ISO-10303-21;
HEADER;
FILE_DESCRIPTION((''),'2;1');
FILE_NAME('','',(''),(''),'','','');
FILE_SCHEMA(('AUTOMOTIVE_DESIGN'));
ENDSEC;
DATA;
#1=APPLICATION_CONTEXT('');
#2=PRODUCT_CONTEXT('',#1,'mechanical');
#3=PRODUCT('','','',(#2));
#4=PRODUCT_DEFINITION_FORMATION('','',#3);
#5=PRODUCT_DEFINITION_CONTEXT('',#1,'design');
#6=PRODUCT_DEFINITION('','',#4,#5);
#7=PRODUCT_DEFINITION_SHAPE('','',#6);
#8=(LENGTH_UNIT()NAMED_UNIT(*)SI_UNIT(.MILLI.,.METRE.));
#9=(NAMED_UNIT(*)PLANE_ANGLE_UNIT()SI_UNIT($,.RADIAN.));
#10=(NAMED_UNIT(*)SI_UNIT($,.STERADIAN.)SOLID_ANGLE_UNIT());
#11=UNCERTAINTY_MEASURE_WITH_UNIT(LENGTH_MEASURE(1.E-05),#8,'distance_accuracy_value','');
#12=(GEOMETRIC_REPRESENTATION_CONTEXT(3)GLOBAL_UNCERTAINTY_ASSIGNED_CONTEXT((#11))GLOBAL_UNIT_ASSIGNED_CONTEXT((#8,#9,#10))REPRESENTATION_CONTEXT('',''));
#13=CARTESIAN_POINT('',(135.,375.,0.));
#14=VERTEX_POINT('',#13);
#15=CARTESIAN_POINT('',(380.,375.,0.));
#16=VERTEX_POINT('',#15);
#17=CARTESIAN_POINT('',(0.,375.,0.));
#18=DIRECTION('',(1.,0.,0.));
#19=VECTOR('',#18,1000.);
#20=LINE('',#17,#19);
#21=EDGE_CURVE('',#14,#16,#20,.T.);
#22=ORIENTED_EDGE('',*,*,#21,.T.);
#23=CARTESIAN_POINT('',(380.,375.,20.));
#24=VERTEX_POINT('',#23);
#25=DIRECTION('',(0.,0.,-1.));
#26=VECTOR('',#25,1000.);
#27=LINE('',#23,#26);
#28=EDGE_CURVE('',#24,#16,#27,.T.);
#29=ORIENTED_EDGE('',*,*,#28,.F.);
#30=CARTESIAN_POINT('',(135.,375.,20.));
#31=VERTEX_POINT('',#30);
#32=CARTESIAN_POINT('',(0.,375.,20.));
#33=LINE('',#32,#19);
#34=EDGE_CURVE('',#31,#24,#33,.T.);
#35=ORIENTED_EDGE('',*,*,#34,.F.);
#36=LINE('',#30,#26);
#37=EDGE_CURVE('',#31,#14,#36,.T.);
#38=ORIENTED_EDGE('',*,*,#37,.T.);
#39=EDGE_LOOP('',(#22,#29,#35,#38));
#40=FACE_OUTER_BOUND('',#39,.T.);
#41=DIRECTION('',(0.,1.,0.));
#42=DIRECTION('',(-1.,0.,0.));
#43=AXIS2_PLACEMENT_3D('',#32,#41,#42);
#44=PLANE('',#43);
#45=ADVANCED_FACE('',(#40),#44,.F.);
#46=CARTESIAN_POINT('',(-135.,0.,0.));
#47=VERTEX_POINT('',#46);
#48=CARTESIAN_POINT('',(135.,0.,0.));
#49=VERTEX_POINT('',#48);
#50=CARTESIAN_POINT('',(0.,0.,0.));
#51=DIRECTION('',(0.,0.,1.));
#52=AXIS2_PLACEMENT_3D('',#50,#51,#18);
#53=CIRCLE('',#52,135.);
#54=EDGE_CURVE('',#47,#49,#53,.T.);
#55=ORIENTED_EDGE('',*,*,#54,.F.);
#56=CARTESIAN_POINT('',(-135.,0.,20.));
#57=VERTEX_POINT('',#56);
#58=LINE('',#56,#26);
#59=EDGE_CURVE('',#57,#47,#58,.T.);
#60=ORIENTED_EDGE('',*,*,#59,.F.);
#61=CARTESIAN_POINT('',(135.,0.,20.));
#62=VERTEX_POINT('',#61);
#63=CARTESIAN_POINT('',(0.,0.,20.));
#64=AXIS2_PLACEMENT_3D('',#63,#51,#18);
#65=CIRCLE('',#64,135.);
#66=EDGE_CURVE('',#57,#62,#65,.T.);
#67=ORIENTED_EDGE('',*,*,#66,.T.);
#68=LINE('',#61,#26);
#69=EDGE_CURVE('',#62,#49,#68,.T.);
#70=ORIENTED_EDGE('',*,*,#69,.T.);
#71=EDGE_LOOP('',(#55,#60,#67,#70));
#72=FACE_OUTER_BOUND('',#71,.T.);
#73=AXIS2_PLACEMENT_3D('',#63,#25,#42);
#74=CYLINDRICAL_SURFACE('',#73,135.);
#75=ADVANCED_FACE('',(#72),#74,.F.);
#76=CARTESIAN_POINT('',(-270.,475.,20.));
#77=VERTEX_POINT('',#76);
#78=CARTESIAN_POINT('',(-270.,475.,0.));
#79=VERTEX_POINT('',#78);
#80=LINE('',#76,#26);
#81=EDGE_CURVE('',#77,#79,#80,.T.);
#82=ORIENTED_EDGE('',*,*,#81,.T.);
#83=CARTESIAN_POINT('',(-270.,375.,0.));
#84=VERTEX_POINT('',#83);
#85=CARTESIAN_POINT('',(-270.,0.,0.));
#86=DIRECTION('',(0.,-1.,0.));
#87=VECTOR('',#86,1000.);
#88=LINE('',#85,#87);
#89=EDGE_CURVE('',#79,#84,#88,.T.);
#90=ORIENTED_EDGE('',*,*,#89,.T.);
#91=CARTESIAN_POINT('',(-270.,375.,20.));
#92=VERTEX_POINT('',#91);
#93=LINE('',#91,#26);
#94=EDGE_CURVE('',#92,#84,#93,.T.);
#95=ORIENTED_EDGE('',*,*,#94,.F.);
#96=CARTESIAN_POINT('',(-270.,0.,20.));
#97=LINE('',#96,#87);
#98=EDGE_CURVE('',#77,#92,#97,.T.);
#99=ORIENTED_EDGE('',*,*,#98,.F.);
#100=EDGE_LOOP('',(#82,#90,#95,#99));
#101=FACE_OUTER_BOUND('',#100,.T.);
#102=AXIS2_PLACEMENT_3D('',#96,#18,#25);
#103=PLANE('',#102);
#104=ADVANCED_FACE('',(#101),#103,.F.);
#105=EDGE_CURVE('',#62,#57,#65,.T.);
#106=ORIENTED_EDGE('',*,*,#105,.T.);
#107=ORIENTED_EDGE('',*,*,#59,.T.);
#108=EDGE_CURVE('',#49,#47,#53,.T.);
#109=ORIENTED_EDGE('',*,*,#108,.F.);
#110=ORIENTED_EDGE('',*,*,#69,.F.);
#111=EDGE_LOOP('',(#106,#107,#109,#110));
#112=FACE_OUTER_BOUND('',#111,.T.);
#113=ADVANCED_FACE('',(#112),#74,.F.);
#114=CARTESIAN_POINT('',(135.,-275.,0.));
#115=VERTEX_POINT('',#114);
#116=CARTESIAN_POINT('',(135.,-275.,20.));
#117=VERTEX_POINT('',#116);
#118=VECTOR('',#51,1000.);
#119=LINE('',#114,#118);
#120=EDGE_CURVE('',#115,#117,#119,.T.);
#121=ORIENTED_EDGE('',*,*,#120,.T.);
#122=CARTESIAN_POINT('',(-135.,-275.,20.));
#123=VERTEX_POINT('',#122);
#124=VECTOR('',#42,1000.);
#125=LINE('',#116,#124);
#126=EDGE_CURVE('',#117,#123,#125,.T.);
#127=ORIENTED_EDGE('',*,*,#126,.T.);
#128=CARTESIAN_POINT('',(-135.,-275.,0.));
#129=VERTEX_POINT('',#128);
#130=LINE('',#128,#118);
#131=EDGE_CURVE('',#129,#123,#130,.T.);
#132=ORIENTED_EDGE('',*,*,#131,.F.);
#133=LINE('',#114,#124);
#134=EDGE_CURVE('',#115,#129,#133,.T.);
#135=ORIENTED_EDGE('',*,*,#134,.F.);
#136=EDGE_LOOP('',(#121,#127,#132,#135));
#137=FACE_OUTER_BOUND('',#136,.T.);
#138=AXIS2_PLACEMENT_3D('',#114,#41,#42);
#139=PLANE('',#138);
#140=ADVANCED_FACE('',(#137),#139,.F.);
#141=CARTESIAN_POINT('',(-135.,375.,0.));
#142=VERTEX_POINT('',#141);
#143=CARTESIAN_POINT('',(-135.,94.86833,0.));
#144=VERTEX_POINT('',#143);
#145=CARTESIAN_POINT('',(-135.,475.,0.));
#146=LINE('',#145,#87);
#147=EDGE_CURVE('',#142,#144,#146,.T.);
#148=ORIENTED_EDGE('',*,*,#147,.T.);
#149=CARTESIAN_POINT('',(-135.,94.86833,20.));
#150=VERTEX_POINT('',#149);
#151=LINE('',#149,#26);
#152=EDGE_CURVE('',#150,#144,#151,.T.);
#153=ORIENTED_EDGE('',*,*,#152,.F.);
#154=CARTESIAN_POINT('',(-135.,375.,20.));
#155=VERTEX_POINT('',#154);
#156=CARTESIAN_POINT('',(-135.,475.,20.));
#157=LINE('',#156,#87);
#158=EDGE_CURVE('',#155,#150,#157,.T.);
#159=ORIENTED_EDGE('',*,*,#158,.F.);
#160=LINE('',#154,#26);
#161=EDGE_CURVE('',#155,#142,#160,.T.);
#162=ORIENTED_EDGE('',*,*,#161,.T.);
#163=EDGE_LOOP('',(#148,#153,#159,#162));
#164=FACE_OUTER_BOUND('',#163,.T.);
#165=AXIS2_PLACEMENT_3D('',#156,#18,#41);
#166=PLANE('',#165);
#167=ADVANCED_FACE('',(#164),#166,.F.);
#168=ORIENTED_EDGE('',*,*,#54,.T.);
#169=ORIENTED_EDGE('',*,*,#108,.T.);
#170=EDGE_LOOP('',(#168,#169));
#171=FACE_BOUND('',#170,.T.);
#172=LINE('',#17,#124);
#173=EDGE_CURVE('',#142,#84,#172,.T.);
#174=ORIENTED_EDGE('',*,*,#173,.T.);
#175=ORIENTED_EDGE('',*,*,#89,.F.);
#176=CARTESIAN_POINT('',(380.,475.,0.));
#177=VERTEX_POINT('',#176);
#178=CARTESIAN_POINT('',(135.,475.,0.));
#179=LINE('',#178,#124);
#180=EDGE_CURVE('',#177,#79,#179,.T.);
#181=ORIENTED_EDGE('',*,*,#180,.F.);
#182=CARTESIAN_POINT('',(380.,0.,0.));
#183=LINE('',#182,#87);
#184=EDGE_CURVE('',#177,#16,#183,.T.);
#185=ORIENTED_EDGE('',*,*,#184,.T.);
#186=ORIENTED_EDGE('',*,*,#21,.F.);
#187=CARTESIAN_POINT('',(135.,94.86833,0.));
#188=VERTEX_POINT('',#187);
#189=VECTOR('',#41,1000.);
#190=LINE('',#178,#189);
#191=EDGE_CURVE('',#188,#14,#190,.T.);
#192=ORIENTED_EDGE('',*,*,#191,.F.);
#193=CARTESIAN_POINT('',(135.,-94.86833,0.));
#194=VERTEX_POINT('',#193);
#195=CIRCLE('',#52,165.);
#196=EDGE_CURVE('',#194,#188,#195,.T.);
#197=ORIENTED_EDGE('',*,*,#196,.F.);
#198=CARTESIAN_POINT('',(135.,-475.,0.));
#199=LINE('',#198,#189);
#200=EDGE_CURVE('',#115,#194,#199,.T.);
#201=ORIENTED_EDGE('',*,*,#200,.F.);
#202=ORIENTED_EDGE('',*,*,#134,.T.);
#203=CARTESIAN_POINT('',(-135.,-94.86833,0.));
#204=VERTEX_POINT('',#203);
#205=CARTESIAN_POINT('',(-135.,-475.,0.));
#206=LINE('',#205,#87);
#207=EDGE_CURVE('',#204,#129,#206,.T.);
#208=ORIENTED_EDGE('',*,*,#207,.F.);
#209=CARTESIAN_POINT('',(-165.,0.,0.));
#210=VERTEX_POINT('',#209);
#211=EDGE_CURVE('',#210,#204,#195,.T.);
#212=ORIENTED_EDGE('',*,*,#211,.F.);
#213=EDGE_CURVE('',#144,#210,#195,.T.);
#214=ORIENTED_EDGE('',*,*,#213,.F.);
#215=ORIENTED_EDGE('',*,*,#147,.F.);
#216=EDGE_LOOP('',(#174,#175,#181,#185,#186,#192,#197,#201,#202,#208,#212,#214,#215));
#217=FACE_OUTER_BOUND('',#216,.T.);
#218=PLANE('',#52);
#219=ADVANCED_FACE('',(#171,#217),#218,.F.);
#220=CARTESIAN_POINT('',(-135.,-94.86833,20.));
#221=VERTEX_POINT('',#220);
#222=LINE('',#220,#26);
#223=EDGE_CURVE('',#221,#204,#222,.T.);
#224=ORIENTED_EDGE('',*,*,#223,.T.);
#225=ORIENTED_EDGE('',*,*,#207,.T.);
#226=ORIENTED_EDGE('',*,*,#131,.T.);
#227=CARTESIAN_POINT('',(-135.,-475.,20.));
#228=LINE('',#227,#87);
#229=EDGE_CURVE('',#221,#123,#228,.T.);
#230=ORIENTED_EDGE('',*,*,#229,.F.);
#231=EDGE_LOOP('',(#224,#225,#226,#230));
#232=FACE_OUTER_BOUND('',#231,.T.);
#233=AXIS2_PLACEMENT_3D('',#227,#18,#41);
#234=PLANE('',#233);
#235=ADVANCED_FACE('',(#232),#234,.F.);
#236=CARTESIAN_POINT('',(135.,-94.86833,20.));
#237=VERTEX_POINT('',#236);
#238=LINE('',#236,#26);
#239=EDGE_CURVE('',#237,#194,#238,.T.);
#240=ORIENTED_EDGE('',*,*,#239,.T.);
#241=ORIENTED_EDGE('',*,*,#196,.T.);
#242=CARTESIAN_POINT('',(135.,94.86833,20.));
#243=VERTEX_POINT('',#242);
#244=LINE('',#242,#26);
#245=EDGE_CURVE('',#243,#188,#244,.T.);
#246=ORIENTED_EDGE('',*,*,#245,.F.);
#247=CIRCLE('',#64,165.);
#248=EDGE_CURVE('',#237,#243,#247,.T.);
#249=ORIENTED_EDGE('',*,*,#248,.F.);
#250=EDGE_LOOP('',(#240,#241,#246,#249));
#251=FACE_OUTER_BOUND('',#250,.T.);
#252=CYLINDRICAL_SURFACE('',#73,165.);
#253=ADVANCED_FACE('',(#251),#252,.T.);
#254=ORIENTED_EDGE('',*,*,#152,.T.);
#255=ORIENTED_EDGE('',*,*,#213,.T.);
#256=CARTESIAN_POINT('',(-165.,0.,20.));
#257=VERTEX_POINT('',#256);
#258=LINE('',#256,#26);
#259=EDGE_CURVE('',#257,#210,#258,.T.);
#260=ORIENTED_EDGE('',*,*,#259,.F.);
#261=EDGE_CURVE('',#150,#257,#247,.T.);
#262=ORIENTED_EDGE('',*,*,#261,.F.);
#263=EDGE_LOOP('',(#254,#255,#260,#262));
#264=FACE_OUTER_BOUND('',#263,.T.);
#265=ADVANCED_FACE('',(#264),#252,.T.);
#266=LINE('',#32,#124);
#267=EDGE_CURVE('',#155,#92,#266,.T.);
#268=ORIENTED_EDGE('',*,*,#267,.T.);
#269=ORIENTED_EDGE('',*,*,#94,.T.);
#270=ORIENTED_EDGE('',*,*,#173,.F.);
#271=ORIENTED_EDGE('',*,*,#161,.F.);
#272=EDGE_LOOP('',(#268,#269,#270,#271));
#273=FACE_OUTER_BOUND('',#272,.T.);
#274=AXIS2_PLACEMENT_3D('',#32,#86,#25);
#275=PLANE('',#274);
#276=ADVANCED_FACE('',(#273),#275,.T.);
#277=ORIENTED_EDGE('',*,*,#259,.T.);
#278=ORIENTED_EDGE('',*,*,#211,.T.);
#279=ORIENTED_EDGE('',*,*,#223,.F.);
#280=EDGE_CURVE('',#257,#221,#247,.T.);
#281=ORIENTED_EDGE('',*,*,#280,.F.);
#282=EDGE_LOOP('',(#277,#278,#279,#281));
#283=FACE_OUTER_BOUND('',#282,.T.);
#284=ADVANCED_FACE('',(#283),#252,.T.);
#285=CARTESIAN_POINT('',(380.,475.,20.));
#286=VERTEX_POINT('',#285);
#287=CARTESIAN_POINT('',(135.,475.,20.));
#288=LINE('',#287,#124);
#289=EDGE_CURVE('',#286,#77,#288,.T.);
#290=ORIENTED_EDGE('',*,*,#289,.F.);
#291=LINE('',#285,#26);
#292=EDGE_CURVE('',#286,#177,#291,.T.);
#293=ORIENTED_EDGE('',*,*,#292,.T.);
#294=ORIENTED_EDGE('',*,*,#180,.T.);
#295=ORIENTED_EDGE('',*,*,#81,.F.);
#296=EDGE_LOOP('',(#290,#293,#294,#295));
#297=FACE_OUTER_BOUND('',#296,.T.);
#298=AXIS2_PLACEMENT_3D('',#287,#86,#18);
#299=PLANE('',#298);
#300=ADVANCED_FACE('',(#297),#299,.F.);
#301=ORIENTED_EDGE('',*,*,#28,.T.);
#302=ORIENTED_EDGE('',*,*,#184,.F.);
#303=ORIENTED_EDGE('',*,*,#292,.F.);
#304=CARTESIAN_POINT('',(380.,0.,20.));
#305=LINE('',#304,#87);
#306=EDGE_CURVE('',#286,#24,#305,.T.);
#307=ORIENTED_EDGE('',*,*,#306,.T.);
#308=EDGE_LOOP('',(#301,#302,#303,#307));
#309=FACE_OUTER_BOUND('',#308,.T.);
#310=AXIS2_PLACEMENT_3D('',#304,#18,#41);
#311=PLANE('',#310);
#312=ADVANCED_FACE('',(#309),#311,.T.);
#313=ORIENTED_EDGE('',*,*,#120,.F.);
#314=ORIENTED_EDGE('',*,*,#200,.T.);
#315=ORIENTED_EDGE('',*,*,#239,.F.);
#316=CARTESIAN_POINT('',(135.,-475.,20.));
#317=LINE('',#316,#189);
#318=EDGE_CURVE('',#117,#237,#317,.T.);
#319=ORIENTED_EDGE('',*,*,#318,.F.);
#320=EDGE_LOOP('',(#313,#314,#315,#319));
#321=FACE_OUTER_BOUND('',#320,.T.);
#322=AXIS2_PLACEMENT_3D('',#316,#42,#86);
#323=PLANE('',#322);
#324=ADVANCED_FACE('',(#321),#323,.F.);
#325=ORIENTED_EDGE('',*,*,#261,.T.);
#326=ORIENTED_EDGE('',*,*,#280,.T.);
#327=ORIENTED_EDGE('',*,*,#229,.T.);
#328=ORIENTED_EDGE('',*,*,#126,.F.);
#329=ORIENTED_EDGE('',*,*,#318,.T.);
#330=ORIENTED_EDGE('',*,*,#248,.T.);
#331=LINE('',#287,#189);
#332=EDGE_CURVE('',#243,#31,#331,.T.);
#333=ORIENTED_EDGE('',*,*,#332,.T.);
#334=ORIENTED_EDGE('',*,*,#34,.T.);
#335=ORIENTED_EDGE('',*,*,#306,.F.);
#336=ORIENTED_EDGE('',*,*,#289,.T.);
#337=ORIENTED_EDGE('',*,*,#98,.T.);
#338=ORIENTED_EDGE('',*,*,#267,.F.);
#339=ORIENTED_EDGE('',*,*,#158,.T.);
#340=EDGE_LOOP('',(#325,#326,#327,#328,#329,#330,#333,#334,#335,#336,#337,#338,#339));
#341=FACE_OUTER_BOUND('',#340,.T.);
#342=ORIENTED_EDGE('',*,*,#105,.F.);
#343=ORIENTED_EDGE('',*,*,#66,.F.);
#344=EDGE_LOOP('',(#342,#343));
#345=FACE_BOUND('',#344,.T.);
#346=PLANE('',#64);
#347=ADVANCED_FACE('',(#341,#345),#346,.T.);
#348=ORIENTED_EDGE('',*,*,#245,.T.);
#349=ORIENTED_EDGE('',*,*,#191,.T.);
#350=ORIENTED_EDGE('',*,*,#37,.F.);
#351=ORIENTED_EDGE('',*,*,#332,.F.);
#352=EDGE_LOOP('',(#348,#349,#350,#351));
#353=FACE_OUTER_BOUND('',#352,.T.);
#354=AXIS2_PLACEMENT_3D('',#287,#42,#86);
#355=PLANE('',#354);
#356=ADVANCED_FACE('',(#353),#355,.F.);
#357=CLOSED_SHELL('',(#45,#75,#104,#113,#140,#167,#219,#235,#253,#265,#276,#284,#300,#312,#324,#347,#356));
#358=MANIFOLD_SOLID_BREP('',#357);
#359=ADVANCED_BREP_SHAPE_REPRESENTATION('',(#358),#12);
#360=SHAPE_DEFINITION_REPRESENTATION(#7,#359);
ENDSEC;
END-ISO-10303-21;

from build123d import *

# Parameters (mm, degrees)
SKETCH1_R           = 135
BOSS_EXTRUDE2_DEPTH = 20
SKETCH5_W           = 270
SKETCH5_H           = 200
CUT_EXTRUDE1_DEPTH  = 20
SKETCH6_W           = 245
SKETCH6_H           = 100
SKETCH6_W_2         = 135
BOSS_EXTRUDE3_DEPTH = 20


with BuildPart() as part:
    # Sketch1 → Boss-Extrude2 (new body)
    with BuildSketch(Plane.XY):
        with BuildLine():
            Line((-135, 475), (-135, 94.868329805))
            ThreePointArc((-135, 94.868329805), (-165, 0), (-135, -94.868329805))
            Line((-135, -94.868329805), (-135, -475))
            Line((-135, -475), (135, -475))
            Line((135, -475), (135, -94.868329805))
            ThreePointArc((135, -94.868329805), (165, 0), (135, 94.868329805))
            Line((135, 94.868329805), (135, 475))
            Line((135, 475), (-135, 475))
        make_face()
        Circle(SKETCH1_R, mode=Mode.SUBTRACT)
    extrude(amount=BOSS_EXTRUDE2_DEPTH)

    # Sketch5 → Cut-Extrude1 (cut)
    with BuildSketch(Plane.XY.offset(20)):
        with Locations((0, -375)):
            Rectangle(SKETCH5_W, SKETCH5_H)
    extrude(amount=-CUT_EXTRUDE1_DEPTH, mode=Mode.SUBTRACT)

    # Sketch6 → Boss-Extrude3 (add)
    with BuildSketch(Plane(origin=(0, 0, 0), x_dir=(-1, 0, 0), z_dir=(0, 0, -1))):
        with Locations((-257.5, 425)):
            Rectangle(SKETCH6_W, SKETCH6_H)
        with Locations((202.5, 425)):
            Rectangle(SKETCH6_W_2, SKETCH6_H)
    extrude(amount=-BOSS_EXTRUDE3_DEPTH)


solid = part.part
